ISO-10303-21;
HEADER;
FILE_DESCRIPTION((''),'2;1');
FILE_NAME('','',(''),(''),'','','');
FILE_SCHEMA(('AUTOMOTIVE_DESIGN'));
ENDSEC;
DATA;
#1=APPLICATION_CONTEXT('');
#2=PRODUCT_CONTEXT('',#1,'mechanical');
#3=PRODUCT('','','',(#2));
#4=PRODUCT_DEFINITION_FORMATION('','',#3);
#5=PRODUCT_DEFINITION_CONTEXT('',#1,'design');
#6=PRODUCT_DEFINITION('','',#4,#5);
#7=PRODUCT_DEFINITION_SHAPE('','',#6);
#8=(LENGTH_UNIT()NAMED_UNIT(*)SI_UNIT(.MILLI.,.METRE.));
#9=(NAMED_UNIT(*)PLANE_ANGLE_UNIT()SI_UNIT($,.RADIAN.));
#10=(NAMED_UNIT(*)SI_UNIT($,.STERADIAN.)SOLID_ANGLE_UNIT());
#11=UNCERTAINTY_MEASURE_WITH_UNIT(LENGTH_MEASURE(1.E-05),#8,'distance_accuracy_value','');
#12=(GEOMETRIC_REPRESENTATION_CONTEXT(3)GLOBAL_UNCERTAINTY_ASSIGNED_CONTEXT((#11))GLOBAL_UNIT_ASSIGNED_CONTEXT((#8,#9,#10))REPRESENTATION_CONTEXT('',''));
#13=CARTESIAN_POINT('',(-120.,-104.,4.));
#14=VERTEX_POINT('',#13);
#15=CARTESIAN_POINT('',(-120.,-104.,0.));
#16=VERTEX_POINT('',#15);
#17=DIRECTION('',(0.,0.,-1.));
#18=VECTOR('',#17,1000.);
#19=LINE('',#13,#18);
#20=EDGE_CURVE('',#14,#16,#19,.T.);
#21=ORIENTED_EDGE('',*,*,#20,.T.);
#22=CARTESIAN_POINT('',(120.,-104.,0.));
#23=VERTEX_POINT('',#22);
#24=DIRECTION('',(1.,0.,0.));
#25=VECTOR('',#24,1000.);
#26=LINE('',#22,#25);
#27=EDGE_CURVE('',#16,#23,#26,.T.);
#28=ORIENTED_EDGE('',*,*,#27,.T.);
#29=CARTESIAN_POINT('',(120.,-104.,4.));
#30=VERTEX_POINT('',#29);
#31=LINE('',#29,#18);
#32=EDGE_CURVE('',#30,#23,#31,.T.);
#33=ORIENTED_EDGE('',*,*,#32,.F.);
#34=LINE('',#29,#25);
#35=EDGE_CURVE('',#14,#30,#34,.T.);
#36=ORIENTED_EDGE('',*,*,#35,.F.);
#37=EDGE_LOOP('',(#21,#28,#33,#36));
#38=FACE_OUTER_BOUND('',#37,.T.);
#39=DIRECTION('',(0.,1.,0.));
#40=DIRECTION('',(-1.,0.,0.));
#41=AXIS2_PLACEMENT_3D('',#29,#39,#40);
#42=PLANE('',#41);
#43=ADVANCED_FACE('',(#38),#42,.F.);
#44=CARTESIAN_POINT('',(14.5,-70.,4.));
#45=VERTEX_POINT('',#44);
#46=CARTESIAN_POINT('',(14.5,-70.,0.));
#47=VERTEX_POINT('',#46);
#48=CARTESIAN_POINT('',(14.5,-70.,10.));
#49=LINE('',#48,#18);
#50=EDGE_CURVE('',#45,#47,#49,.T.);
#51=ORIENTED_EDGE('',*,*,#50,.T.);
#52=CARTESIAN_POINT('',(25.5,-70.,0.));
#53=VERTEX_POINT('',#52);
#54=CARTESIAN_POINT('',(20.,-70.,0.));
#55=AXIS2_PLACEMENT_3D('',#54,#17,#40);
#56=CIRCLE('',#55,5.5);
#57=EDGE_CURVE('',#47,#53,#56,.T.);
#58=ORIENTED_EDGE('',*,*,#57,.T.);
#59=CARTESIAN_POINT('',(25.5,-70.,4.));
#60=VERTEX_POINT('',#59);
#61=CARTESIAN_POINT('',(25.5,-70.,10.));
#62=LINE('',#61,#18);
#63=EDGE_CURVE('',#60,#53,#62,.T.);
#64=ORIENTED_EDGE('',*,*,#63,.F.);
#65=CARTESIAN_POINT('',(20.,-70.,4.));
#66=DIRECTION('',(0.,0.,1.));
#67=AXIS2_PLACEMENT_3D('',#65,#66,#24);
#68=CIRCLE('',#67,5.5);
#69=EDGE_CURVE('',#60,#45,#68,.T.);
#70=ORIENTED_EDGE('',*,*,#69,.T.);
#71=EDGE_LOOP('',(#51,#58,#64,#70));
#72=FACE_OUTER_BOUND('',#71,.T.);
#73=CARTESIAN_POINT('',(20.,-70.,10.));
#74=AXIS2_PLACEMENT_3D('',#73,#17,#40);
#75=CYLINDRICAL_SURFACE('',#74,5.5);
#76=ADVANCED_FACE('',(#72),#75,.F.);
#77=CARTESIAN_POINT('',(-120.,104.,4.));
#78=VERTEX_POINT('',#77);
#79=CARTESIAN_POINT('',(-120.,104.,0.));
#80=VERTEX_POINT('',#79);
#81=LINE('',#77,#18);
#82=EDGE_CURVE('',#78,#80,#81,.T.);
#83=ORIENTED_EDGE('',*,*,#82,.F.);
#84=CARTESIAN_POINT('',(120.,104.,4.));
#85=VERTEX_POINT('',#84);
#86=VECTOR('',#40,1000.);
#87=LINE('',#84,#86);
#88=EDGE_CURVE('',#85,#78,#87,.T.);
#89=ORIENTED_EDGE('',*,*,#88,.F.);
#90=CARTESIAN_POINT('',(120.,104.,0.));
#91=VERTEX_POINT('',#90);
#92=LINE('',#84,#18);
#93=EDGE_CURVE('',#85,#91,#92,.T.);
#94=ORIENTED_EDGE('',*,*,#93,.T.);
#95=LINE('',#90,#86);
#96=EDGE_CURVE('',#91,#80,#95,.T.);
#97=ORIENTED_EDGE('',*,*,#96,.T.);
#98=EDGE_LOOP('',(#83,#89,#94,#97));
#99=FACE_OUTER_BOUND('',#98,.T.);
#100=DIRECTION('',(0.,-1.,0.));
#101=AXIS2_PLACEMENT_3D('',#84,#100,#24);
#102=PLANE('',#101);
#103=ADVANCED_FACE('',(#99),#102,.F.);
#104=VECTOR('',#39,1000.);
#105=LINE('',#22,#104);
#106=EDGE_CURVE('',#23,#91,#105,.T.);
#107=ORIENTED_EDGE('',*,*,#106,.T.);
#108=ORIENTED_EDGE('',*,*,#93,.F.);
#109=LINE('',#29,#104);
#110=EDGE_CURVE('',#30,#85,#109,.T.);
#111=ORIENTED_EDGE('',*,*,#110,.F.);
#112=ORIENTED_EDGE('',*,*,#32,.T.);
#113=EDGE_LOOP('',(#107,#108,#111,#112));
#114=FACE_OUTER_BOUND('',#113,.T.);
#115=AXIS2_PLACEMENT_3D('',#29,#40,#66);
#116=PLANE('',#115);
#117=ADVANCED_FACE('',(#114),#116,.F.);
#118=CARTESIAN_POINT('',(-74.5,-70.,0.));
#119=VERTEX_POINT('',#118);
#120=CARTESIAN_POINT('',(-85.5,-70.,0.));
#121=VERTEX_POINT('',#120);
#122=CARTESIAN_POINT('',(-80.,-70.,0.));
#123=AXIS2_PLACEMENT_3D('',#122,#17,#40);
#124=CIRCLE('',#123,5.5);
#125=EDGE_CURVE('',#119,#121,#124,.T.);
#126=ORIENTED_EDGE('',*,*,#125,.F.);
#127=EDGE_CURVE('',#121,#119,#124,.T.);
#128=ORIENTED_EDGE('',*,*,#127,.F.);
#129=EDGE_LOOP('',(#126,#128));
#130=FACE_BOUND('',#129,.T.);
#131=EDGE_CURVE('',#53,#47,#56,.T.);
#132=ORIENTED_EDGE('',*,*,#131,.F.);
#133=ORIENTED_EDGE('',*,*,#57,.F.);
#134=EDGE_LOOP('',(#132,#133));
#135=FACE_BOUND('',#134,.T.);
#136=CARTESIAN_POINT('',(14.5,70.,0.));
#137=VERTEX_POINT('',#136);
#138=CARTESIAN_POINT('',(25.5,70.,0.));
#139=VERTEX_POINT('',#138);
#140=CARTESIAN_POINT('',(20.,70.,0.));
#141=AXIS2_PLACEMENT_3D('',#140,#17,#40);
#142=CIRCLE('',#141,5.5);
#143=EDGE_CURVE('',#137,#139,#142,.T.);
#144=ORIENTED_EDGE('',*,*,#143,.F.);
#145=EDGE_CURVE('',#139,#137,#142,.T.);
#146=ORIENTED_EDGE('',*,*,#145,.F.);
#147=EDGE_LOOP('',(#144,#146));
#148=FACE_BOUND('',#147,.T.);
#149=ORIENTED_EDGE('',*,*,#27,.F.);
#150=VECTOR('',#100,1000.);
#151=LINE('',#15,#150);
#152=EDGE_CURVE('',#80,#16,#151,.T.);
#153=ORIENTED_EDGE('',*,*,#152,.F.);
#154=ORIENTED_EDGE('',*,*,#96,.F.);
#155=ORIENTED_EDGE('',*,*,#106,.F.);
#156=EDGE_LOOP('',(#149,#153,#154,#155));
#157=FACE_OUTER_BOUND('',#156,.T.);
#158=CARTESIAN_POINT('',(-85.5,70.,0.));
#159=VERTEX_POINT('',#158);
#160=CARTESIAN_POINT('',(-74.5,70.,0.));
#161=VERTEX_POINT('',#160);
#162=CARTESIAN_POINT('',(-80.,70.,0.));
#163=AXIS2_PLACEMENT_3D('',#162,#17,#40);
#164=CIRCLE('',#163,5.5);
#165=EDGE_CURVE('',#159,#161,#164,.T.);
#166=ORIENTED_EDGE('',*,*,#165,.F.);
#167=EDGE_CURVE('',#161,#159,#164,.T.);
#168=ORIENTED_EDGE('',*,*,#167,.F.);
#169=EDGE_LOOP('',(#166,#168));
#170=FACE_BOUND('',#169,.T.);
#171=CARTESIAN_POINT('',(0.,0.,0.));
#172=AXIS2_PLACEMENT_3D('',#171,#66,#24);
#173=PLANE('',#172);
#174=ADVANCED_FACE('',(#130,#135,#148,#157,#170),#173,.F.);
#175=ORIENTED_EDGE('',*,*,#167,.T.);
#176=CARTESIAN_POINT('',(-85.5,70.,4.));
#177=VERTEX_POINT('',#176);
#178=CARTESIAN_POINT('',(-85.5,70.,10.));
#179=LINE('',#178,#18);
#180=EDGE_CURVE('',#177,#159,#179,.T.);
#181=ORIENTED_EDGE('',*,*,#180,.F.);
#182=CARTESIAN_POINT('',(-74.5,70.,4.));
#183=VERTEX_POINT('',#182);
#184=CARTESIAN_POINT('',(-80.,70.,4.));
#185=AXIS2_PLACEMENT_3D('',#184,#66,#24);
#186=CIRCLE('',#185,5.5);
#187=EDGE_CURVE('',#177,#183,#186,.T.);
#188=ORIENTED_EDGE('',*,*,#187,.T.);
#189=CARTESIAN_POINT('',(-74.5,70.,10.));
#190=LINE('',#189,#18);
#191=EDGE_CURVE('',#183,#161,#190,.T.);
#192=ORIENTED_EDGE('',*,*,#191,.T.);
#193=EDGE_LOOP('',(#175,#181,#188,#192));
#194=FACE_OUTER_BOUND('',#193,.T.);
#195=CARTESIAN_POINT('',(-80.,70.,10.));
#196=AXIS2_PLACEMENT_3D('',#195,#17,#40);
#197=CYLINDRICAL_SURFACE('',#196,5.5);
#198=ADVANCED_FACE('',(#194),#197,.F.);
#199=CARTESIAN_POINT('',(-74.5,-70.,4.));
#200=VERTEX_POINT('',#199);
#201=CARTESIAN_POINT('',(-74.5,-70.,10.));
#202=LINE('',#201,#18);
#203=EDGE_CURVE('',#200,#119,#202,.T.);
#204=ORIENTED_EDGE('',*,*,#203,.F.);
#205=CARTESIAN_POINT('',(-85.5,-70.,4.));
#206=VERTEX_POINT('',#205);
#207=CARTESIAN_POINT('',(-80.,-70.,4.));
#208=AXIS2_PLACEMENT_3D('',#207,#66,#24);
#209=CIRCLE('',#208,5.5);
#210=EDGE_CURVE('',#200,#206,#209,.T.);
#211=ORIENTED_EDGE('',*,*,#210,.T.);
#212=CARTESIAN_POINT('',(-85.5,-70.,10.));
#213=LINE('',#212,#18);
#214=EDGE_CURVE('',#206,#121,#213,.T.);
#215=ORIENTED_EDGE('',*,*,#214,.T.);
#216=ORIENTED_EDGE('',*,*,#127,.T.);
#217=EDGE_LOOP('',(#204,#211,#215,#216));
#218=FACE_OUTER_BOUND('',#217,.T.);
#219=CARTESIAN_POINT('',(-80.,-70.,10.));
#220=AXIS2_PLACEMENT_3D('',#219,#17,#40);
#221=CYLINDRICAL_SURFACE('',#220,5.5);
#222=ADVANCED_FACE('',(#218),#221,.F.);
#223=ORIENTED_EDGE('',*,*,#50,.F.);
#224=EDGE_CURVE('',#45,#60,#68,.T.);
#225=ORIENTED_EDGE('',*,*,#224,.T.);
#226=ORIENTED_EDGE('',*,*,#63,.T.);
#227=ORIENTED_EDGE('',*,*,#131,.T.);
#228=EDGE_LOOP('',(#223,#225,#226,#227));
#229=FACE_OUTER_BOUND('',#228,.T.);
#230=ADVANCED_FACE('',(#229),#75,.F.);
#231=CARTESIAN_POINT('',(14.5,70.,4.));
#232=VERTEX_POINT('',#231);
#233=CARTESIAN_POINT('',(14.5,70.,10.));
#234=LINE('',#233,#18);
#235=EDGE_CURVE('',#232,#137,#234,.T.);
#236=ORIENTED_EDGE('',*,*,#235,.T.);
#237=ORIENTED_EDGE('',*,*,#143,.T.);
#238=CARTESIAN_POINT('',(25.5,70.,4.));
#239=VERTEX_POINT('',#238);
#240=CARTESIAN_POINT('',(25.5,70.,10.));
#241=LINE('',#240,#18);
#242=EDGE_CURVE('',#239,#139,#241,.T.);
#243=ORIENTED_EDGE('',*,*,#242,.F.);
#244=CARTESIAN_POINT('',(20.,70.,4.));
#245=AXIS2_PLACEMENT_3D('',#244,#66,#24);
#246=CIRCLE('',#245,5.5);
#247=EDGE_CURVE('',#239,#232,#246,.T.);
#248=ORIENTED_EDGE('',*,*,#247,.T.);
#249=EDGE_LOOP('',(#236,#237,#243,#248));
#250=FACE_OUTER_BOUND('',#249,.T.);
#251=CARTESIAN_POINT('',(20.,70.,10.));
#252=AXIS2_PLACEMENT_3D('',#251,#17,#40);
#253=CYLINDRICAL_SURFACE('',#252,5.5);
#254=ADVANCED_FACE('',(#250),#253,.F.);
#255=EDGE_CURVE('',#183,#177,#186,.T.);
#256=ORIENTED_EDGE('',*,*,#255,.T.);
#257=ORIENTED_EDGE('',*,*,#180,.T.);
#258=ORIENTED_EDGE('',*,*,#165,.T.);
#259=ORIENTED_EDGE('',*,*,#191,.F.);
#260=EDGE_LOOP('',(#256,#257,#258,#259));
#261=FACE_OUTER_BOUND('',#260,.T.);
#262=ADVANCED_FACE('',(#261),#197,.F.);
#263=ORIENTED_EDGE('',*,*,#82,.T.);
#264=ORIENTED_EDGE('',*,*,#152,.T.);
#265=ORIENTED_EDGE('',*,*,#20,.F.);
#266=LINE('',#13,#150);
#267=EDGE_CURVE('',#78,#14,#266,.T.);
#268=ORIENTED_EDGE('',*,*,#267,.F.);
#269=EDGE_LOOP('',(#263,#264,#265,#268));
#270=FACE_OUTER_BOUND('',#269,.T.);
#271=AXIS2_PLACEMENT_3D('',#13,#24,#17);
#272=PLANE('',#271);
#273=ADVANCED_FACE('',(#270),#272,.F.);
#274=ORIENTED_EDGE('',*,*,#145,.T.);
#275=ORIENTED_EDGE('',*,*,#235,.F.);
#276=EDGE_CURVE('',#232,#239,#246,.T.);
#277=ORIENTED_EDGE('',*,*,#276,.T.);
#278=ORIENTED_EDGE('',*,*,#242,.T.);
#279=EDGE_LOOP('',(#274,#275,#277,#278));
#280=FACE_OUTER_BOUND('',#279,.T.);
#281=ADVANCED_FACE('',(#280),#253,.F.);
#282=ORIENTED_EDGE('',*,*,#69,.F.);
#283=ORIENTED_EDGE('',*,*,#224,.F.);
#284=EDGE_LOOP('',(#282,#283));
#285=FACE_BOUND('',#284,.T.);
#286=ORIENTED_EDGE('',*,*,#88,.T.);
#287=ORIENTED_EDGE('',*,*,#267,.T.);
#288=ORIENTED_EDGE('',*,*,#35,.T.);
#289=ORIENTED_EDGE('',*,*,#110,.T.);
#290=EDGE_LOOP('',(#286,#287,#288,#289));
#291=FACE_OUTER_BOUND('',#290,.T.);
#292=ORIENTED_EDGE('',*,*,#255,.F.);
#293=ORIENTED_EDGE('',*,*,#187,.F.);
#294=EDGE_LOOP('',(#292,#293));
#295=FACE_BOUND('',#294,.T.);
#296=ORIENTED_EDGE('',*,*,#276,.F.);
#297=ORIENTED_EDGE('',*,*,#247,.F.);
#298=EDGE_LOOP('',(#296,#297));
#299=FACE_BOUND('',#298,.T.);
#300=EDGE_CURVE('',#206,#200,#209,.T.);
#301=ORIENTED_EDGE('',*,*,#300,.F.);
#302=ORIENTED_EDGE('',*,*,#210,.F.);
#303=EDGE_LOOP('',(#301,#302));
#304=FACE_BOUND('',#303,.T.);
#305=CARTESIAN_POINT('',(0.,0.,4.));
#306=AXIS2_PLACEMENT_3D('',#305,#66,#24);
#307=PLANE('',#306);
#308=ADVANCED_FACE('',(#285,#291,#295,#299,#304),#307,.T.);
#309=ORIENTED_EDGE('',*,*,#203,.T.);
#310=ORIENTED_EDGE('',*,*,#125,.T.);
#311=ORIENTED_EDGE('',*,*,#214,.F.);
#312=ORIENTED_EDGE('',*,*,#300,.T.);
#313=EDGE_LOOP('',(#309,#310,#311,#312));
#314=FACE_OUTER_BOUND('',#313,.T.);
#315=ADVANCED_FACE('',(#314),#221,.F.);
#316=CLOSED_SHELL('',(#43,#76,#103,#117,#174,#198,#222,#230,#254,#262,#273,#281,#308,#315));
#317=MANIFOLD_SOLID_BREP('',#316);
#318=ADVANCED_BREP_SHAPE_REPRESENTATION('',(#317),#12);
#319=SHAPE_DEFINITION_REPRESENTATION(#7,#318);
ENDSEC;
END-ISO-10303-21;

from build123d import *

# Parameters (mm, degrees)
SKETCH_1_W          = 240
SKETCH_1_H          = 208
EXTRUDE_1_DEPTH     = 4
SKETCH_2_R          = 5.5
CUT_EXTRUDE_1_DEPTH = 10


with BuildPart() as part:
    # 草图1 → 凸台-拉伸1 (new body)
    with BuildSketch(Plane.XY):
        Rectangle(SKETCH_1_W, SKETCH_1_H)
    extrude(amount=EXTRUDE_1_DEPTH)

    # 草图2 → 切除-拉伸1 (cut)
    with BuildSketch(Plane(origin=(0, 0, 0), x_dir=(-1, 0, 0), z_dir=(0, 0, -1))):
        with Locations((-20, -70)):
            Circle(SKETCH_2_R)
        with Locations((80, -70)):
            Circle(SKETCH_2_R)
        with Locations((80, 70)):
            Circle(SKETCH_2_R)
        with Locations((-20, 70)):
            Circle(SKETCH_2_R)
    extrude(amount=-CUT_EXTRUDE_1_DEPTH, mode=Mode.SUBTRACT)


solid = part.part
